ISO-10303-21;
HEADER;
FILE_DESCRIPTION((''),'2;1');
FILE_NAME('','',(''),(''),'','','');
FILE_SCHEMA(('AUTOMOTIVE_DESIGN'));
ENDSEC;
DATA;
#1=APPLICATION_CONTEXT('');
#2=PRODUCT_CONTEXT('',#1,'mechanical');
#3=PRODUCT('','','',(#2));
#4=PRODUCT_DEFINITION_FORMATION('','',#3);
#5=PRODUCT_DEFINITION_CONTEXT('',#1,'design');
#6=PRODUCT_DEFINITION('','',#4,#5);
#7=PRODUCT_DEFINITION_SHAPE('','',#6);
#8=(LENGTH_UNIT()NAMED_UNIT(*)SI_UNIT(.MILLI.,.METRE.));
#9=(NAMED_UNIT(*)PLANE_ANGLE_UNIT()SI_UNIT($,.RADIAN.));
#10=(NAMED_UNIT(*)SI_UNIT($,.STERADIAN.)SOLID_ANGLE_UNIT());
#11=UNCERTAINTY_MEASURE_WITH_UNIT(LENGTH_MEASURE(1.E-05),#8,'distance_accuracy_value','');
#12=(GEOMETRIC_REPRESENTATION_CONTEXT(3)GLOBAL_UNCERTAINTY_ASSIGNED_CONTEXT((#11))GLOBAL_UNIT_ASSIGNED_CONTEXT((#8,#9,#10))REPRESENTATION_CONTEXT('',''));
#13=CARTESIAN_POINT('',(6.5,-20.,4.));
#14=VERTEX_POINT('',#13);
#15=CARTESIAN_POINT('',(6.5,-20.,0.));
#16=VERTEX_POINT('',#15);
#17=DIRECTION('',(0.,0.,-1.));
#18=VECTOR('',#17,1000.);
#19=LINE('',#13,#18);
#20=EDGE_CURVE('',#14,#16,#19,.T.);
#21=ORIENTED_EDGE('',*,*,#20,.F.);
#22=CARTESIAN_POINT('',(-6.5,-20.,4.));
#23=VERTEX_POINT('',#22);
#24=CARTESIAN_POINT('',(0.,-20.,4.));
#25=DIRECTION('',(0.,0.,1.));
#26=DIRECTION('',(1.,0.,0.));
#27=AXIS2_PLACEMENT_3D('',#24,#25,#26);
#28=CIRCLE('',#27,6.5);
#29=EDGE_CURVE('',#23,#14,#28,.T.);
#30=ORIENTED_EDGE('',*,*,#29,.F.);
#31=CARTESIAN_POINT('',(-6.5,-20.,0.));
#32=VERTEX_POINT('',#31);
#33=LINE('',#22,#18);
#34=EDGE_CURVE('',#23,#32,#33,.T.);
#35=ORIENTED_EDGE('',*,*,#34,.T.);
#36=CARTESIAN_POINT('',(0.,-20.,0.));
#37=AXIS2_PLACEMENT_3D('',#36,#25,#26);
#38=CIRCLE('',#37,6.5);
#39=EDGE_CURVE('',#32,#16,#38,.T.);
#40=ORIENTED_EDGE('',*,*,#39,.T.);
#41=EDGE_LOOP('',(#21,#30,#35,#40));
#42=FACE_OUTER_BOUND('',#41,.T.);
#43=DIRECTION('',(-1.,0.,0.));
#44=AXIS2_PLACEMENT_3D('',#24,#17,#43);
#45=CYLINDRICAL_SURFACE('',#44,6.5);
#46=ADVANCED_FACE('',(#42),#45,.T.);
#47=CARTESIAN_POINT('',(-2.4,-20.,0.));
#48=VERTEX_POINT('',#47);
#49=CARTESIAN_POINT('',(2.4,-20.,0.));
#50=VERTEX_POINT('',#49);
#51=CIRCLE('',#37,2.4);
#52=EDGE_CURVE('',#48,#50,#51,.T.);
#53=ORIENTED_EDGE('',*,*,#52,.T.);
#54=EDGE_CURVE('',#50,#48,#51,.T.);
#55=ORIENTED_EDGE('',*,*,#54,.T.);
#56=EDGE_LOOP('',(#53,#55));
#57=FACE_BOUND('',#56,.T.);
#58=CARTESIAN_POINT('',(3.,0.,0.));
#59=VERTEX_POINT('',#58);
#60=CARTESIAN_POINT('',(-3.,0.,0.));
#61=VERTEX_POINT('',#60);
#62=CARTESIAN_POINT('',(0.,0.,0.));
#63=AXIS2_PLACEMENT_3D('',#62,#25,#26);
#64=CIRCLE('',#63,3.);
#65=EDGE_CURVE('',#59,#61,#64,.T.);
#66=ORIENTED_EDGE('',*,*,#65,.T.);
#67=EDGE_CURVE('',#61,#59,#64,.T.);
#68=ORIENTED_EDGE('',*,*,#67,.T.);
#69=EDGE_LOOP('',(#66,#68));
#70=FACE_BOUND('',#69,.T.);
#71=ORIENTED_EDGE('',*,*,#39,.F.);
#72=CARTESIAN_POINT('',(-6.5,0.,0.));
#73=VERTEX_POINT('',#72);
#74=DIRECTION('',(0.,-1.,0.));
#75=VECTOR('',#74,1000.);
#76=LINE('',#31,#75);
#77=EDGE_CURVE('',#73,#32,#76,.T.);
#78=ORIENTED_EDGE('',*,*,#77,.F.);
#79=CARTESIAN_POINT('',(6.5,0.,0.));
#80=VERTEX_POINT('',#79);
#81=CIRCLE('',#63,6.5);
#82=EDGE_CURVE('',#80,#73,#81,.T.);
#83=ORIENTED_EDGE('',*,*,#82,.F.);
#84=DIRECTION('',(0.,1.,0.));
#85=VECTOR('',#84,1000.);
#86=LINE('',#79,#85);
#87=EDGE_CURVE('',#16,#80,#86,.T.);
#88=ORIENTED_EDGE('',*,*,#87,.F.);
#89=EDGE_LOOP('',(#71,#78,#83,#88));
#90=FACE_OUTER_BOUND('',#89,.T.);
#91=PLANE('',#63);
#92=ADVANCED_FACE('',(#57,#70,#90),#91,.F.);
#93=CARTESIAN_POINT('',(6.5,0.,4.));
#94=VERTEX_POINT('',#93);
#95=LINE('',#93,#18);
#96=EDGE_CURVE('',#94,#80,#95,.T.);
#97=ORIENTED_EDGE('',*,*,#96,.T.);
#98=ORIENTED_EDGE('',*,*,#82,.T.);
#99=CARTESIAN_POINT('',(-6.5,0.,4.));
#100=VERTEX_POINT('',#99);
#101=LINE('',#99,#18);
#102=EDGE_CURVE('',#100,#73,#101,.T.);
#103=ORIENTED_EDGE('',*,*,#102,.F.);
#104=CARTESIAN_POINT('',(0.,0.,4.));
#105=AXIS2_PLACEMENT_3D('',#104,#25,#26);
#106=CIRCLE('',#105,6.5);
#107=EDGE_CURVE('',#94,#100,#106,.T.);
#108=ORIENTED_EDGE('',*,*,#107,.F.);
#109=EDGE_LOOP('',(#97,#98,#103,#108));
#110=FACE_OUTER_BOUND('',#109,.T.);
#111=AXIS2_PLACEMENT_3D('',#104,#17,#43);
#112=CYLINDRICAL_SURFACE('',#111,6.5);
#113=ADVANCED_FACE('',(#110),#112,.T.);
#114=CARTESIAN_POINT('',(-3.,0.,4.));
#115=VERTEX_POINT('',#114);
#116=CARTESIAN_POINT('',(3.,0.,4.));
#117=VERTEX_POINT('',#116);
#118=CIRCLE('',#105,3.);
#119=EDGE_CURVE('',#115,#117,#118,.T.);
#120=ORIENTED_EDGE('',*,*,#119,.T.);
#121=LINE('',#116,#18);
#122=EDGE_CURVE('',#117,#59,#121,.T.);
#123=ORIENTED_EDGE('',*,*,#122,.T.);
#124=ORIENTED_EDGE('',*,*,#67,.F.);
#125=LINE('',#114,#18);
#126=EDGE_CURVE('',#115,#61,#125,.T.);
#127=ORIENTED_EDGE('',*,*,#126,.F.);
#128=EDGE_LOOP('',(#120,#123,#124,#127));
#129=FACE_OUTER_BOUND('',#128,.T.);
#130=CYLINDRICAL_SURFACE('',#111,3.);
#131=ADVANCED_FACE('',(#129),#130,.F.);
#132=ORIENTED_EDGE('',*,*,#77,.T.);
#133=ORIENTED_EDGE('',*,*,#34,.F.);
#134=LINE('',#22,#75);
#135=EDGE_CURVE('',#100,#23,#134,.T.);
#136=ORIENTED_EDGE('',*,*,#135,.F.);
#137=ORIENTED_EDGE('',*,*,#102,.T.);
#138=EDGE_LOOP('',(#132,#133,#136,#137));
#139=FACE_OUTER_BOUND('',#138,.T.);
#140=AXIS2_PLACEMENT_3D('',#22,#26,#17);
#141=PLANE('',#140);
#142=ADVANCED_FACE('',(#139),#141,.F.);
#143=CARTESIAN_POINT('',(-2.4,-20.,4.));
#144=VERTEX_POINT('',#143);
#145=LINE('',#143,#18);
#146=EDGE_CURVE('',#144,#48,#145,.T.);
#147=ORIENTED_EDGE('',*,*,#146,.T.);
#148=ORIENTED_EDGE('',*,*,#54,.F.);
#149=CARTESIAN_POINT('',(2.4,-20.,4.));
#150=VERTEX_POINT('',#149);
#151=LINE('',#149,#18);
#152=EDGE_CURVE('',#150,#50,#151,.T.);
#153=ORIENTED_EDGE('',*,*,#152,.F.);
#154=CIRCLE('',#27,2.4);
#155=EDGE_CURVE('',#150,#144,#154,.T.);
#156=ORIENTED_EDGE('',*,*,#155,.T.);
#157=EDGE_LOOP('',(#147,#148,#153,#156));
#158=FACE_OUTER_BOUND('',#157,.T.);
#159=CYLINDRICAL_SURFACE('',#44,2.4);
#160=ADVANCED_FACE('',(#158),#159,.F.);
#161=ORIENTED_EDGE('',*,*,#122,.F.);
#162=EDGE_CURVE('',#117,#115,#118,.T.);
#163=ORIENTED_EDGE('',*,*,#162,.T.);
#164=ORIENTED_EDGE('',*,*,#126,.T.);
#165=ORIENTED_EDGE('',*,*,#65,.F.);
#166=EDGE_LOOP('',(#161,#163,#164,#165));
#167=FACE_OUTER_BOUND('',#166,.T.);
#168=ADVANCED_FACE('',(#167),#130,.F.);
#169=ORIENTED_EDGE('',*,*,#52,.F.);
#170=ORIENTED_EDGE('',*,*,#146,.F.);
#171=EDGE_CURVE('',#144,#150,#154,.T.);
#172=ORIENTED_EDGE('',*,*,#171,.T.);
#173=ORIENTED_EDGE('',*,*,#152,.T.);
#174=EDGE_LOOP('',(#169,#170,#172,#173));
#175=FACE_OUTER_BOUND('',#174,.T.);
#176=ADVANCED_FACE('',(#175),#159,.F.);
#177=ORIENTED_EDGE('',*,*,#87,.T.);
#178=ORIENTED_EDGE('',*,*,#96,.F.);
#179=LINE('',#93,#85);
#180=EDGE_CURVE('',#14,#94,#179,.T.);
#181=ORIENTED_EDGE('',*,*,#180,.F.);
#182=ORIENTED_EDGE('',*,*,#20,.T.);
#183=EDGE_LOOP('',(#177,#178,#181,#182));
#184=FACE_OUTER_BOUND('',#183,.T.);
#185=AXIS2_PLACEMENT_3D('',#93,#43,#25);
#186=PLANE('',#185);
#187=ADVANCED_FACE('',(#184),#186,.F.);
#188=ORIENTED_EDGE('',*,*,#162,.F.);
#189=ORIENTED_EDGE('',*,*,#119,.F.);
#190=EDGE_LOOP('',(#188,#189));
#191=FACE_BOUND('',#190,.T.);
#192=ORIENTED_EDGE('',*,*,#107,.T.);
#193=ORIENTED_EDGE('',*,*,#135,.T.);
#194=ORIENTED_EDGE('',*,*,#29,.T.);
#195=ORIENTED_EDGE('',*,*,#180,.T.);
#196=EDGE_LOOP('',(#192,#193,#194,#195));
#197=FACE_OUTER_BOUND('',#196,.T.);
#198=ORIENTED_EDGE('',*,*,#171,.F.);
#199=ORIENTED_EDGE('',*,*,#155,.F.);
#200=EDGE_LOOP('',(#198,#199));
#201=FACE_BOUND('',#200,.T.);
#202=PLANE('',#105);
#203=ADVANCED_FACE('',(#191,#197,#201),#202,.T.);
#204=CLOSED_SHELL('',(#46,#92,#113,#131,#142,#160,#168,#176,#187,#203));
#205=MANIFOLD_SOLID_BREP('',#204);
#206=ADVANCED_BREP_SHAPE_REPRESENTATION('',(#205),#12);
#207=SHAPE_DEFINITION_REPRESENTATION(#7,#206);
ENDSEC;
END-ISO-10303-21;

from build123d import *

# Parameters (mm, degrees)
SKETCH1_R           = 3
SKETCH1_R_2         = 2.4
BOSS_EXTRUDE1_DEPTH = 4


with BuildPart() as part:
    # Sketch1 → Boss-Extrude1 (new body)
    with BuildSketch(Plane.XY):
        with BuildLine():
            Line((6.5, 0), (6.5, -20))
            ThreePointArc((6.5, -20), (0, -26.5), (-6.5, -20))
            Line((-6.5, -20), (-6.5, 0))
            ThreePointArc((-6.5, 0), (0, 6.5), (6.5, 0))
        make_face()
        Circle(SKETCH1_R, mode=Mode.SUBTRACT)
        with Locations((0, -20)):
            Circle(SKETCH1_R_2, mode=Mode.SUBTRACT)
    extrude(amount=BOSS_EXTRUDE1_DEPTH)


solid = part.part
